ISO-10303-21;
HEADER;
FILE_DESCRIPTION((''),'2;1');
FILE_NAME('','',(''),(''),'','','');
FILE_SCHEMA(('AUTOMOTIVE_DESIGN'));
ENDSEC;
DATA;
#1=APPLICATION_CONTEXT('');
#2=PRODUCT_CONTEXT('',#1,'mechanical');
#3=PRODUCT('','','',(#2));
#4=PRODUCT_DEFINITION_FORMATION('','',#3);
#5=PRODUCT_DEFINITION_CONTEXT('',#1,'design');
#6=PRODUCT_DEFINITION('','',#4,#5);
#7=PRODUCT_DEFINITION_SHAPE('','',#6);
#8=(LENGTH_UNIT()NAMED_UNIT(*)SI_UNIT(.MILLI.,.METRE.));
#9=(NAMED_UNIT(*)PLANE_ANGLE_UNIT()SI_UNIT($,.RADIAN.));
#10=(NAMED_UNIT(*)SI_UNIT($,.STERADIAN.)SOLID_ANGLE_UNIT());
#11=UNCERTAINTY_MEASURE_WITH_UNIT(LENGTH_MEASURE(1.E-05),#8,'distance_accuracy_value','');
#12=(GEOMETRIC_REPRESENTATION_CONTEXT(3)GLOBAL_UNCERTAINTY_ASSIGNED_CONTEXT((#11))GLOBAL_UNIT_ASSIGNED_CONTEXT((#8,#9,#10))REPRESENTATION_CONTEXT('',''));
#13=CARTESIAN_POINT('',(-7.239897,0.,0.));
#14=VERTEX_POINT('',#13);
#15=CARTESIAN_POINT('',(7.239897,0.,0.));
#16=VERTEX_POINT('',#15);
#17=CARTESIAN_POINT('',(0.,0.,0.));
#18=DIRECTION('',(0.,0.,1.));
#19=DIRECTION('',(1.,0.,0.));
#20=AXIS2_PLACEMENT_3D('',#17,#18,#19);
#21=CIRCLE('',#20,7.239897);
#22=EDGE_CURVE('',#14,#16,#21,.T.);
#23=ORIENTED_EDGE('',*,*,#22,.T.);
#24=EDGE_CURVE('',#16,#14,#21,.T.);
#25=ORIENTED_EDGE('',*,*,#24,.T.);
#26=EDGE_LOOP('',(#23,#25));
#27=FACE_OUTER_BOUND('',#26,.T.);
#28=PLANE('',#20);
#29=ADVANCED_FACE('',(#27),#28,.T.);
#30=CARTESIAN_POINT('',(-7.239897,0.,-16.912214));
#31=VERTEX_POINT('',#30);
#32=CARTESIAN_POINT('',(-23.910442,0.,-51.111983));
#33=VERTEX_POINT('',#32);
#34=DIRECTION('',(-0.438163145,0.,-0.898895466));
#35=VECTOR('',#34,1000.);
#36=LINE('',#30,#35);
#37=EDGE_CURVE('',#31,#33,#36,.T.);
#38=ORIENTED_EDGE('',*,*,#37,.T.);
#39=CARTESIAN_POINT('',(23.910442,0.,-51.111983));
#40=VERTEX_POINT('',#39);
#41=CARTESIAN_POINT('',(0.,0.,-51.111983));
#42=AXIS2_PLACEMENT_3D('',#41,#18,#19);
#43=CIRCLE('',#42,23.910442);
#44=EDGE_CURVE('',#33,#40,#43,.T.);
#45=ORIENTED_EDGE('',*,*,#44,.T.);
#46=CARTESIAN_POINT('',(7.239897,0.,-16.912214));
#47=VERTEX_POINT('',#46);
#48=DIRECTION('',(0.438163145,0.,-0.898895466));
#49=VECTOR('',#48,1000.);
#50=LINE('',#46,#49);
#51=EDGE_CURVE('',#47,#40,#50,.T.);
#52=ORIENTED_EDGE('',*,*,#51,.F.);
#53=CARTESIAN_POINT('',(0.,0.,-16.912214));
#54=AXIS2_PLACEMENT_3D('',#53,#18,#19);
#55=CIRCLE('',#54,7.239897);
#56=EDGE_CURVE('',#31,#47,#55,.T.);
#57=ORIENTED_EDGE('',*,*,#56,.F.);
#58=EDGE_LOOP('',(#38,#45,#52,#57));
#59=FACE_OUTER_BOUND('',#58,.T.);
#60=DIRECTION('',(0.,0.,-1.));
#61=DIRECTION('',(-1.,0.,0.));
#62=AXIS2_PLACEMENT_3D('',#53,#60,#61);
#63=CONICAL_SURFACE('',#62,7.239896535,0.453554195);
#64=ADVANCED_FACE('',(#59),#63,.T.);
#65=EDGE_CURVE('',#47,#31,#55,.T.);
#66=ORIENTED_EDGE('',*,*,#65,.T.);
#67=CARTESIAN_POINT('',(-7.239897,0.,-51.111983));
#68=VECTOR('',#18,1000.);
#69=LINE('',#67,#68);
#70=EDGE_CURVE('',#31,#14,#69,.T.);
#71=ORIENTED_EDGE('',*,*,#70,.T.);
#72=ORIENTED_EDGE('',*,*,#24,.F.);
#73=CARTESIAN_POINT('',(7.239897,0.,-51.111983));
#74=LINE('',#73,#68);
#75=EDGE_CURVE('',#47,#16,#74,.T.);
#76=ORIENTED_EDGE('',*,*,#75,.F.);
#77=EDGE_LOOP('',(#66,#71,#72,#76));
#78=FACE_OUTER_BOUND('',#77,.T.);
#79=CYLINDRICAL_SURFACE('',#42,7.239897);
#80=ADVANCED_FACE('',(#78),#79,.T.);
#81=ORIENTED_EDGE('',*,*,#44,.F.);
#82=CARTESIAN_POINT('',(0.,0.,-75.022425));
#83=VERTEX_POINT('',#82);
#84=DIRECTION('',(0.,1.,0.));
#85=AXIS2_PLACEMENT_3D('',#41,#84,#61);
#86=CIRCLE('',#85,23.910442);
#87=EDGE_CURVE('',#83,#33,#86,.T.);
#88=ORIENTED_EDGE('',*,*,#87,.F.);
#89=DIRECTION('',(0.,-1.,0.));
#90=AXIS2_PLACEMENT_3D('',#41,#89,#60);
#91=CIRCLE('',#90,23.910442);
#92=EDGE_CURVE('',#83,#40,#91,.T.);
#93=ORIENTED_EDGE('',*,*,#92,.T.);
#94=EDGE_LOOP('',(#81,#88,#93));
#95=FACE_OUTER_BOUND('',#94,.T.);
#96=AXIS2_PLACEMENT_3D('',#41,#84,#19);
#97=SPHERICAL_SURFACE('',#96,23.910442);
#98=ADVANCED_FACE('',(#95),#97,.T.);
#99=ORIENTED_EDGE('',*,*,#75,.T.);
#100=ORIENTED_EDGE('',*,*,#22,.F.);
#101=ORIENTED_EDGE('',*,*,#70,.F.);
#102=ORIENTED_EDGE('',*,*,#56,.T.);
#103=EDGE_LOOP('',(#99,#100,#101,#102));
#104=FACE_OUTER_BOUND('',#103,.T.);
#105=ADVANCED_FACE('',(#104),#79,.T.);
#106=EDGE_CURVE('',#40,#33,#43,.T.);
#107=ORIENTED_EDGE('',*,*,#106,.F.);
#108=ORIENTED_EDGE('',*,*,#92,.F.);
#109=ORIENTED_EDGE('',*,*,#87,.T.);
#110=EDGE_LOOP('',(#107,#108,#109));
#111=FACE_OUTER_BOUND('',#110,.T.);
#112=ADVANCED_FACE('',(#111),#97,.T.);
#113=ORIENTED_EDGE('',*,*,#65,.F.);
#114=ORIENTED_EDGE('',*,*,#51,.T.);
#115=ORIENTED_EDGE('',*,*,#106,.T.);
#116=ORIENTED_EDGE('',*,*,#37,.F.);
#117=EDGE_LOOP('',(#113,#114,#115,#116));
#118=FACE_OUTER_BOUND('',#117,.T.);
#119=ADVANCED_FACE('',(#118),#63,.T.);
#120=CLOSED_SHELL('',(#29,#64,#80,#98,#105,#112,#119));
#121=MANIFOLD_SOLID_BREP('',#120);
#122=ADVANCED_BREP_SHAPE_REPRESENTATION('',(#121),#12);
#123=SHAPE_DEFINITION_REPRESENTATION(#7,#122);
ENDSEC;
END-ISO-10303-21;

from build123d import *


with BuildPart() as part:
    # Sketch1 → Revolve1 (revolve)
    with BuildSketch(Plane(origin=(0, 0, 0), x_dir=(1, 0, 0), z_dir=(0, 1, 0))):
        with BuildLine():
            Line((0, 0), (7.239896535, 0))
            Line((7.239896535, 0), (7.239896535, 16.912213927))
            Line((7.239896535, 16.912213927), (23.910442474, 51.11198251))
            ThreePointArc((23.910442474, 51.11198251), (16.907236015, 68.019218524), (0, 75.022424984))
            Line((0, 75.022424984), (0, 51.11198251))
            Line((0, 51.11198251), (0, 0))
        make_face()
    revolve(axis=Axis((0, 0, -51.11198251), (0, 0, -1)))


solid = part.part
